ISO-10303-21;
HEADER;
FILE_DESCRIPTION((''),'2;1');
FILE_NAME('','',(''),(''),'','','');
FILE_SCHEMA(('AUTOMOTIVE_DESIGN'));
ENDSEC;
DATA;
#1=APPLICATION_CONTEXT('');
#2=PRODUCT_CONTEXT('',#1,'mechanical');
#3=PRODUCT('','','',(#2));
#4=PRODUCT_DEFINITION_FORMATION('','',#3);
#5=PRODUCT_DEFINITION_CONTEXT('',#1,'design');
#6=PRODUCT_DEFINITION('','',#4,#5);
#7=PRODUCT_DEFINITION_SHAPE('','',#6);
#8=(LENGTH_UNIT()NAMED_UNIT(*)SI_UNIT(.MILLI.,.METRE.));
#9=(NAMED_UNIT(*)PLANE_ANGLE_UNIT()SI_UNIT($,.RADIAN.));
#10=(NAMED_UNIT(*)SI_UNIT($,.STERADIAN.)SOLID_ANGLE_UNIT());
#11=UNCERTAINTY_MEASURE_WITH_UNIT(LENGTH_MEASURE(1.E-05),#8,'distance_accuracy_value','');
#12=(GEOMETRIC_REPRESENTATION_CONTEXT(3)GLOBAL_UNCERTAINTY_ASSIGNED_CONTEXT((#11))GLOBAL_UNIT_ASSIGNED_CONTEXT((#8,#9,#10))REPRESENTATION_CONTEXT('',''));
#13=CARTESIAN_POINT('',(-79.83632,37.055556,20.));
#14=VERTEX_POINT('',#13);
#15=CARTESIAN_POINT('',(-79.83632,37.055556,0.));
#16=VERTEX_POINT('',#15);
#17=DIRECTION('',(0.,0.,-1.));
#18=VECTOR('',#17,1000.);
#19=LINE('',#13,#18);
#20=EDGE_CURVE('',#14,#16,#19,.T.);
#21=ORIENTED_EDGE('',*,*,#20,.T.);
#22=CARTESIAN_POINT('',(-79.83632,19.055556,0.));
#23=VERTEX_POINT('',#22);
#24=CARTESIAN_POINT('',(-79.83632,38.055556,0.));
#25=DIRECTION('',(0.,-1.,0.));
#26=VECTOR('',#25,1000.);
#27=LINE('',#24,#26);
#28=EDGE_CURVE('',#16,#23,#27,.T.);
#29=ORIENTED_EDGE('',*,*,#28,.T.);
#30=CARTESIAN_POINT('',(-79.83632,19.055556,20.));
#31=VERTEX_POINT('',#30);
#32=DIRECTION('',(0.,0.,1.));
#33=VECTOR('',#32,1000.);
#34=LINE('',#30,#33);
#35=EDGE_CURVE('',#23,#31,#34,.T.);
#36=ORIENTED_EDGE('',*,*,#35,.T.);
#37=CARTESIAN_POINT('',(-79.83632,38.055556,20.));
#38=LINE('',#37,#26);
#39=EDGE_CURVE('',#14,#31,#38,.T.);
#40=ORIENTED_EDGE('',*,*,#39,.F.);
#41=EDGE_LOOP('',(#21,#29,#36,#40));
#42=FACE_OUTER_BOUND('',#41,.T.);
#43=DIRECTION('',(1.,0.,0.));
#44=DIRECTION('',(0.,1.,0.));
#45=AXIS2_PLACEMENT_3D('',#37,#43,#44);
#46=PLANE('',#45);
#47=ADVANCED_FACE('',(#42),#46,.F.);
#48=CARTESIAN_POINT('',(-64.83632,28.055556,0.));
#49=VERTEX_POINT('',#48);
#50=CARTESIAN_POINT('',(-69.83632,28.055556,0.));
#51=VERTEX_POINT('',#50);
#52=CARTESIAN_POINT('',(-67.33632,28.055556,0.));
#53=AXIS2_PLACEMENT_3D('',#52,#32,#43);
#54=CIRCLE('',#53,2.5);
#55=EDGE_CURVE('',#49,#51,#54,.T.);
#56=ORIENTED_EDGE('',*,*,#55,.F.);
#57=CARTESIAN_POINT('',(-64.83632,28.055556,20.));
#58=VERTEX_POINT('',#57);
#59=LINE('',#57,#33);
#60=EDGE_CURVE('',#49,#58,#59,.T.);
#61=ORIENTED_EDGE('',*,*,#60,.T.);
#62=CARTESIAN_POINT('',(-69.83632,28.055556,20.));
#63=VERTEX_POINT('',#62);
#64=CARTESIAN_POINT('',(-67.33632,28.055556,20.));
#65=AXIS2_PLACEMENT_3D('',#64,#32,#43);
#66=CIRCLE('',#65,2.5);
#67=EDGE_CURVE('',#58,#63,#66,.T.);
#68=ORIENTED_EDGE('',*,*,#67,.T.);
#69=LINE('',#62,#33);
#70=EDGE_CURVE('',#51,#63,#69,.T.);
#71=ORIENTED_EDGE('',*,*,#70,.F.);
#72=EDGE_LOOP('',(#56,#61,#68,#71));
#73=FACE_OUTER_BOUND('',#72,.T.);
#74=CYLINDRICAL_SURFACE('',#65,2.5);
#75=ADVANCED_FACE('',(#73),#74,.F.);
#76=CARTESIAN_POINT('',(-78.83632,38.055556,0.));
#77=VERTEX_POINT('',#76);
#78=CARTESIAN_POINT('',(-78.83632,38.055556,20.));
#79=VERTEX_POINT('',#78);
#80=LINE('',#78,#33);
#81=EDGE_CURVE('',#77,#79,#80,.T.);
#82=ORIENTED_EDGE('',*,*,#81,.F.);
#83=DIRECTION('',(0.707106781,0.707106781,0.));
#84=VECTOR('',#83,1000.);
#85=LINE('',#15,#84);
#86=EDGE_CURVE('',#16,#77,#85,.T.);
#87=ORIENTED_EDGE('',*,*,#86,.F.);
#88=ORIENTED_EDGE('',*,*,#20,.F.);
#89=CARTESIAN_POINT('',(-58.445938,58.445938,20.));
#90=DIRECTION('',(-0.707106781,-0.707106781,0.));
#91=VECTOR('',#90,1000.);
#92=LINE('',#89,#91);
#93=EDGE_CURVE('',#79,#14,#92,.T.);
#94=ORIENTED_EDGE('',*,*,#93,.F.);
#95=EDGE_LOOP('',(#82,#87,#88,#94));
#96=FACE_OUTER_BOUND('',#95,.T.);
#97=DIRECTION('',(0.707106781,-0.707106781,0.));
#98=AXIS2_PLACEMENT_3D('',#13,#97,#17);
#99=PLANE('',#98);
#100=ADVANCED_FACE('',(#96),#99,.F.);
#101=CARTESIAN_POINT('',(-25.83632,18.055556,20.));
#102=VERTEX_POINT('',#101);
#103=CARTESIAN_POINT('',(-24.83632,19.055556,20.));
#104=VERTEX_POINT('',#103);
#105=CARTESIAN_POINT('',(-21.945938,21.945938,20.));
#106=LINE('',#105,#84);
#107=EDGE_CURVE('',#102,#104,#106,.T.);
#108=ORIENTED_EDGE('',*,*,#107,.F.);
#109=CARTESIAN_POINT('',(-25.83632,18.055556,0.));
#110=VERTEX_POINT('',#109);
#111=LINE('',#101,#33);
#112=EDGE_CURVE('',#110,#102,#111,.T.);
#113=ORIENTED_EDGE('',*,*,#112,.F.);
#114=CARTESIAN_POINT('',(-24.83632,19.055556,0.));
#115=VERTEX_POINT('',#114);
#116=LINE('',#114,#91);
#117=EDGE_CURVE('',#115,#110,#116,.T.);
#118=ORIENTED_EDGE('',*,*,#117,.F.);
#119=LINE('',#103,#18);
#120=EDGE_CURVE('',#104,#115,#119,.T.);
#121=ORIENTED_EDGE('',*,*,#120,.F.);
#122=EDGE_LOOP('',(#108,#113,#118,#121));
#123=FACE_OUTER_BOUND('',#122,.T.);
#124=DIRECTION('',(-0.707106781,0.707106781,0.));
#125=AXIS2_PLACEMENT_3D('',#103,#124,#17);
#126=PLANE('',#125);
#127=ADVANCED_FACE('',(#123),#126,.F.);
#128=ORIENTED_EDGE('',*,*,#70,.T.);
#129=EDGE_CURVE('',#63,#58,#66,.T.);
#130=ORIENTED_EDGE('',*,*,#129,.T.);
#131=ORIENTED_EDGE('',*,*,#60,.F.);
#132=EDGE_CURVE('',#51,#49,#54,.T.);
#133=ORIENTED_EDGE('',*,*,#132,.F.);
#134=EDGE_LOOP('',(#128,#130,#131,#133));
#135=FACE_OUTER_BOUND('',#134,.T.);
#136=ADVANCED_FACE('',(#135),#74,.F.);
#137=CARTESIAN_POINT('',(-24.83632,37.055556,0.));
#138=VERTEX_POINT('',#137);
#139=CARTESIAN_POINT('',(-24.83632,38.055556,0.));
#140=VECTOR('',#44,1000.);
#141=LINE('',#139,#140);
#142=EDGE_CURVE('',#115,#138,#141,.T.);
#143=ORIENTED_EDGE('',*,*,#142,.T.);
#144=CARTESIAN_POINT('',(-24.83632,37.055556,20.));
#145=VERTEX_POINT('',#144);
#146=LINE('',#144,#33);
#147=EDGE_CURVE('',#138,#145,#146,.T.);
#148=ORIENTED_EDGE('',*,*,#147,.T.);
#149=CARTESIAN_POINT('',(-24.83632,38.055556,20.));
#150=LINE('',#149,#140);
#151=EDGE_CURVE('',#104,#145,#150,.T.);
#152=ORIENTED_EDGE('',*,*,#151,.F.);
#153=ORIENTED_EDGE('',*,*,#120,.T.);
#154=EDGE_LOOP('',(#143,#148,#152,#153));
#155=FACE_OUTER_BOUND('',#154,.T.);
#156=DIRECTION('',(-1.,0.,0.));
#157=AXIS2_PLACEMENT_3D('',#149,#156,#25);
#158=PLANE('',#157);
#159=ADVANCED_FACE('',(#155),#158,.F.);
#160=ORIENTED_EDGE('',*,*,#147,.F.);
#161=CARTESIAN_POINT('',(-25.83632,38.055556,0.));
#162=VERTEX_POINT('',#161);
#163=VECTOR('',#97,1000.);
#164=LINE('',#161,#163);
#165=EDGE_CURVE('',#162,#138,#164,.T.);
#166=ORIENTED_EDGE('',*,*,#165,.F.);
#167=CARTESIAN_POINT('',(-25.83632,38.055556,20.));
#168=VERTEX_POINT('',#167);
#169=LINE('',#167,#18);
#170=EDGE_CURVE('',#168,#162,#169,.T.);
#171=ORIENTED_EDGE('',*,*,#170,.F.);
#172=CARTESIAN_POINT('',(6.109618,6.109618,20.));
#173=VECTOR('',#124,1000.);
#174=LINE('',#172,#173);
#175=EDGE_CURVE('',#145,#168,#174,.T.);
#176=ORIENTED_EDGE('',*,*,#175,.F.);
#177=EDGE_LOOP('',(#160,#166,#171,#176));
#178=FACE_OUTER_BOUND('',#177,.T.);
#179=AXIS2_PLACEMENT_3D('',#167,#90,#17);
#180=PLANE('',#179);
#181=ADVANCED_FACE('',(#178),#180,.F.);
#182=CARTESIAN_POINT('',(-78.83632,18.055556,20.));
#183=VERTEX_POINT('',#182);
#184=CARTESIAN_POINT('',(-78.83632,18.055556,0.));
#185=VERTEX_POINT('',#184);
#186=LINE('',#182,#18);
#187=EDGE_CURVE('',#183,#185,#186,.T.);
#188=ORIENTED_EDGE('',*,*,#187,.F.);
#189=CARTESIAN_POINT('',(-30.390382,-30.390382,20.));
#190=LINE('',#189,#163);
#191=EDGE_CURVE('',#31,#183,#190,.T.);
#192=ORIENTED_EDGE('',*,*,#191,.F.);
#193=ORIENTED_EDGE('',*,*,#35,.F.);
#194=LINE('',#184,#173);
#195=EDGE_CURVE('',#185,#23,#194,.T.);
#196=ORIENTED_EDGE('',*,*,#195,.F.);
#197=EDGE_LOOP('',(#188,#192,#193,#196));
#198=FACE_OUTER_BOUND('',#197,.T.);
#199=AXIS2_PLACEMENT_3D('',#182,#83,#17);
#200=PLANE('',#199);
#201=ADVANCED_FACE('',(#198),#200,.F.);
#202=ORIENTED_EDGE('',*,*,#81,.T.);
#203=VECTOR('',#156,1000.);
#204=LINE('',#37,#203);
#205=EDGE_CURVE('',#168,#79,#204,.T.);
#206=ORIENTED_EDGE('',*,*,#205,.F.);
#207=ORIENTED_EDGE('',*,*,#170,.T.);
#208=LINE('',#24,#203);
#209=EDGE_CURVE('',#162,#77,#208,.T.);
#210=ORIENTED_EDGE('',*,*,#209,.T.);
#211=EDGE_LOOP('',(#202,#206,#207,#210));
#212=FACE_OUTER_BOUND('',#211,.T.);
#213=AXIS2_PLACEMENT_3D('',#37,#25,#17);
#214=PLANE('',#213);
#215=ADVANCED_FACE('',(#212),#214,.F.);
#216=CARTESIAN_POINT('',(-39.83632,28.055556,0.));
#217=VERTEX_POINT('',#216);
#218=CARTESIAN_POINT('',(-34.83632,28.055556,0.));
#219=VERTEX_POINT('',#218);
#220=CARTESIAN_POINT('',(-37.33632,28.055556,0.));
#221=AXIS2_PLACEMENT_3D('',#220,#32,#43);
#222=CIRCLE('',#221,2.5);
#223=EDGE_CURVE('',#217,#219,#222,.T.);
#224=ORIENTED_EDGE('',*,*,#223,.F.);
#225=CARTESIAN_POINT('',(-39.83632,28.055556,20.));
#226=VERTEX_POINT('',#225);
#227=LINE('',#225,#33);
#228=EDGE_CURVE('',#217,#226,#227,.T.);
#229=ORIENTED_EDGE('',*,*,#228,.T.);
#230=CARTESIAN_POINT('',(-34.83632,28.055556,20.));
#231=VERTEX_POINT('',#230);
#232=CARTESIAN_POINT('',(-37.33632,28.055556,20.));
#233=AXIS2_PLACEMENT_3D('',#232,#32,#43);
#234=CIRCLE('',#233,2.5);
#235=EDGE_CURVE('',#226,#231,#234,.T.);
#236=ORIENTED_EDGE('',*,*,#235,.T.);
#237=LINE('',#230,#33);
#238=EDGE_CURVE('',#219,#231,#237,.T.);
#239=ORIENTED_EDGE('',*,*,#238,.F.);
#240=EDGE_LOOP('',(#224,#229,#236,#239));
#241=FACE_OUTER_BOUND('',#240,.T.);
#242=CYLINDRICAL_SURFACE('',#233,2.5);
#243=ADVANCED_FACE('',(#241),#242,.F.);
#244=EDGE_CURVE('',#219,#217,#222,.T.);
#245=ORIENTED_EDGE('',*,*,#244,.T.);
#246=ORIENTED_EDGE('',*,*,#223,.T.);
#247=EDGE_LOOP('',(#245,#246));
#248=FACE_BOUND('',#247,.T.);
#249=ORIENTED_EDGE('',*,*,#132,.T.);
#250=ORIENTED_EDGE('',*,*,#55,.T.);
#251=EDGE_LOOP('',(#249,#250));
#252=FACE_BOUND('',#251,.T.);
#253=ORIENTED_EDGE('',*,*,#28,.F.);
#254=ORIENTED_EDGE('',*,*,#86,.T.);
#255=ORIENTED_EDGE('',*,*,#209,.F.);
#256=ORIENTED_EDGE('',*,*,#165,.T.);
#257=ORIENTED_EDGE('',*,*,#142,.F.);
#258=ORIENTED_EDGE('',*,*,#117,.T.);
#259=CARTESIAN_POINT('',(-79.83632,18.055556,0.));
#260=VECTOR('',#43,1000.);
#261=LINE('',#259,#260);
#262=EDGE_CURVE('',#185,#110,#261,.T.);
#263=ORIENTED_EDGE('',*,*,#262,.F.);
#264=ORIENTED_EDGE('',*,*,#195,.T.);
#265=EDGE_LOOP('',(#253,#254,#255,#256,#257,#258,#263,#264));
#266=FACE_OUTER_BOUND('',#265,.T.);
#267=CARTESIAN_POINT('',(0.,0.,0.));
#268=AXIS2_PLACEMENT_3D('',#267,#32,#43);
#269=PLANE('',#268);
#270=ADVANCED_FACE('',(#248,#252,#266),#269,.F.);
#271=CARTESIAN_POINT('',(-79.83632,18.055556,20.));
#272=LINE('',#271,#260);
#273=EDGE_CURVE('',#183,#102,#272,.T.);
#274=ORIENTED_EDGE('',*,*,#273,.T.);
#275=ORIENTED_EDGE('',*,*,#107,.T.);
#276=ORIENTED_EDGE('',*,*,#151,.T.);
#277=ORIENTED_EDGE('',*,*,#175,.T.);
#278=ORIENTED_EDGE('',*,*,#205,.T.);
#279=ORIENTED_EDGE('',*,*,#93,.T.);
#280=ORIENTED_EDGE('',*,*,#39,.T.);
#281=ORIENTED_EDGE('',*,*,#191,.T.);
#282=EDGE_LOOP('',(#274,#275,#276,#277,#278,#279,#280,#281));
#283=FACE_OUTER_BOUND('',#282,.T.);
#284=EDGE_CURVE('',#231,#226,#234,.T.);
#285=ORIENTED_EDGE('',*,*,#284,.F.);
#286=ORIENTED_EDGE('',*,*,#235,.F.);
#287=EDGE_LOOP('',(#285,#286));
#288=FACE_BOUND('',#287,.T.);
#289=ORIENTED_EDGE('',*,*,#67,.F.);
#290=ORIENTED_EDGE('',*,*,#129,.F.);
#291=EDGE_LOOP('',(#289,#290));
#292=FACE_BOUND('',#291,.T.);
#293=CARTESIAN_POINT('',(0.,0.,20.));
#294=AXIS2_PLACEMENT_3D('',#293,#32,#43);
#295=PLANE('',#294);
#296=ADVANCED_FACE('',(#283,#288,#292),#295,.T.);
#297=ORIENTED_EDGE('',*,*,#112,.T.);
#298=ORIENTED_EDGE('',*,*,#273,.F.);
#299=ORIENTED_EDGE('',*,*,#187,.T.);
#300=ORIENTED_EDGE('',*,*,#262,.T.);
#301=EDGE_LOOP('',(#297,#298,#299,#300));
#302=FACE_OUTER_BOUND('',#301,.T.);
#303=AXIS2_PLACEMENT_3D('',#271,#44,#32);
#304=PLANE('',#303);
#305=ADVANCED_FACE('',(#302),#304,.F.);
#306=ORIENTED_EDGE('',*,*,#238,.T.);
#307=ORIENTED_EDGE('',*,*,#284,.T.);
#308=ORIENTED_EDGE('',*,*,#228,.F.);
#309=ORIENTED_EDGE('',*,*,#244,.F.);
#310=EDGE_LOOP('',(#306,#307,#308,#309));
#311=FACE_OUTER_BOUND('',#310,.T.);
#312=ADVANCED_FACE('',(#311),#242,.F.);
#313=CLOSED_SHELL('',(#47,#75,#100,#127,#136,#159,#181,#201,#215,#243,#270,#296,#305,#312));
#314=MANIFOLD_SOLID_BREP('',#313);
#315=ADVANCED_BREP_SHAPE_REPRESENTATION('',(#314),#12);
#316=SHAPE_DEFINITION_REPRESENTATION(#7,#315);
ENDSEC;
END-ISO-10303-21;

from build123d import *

# Parameters (mm, degrees)
SKETCH1_W           = 55
SKETCH1_H           = 20
BOSS_EXTRUDE1_DEPTH = 20
M6_TAPPED_HOLE1_D   = 5
CHAMFER1_SIZE       = 1


with BuildPart() as part:
    # Sketch1 → Boss-Extrude1 (new body)
    with BuildSketch(Plane.XY):
        with Locations((-52.336320298, 28.055555556)):
            Rectangle(SKETCH1_W, SKETCH1_H)
    extrude(amount=BOSS_EXTRUDE1_DEPTH)

    # M6 Tapped Hole1 (through all)
    with Locations(Plane.XY.offset(20)):
        with Locations((-67.336320298, 28.055555556), (-37.336320298, 28.055555556)):
            Hole(M6_TAPPED_HOLE1_D / 2)

    # Chamfer1
    chamfer1_edges = [part.edges().sort_by_distance(p)[0] for p in [
        (-79.836320298, 38.055555556, 10),
        (-24.836320298, 38.055555556, 10),
        (-24.836320298, 18.055555556, 10),
        (-79.836320298, 18.055555556, 10),
    ]]
    chamfer(chamfer1_edges, length=CHAMFER1_SIZE)


solid = part.part
